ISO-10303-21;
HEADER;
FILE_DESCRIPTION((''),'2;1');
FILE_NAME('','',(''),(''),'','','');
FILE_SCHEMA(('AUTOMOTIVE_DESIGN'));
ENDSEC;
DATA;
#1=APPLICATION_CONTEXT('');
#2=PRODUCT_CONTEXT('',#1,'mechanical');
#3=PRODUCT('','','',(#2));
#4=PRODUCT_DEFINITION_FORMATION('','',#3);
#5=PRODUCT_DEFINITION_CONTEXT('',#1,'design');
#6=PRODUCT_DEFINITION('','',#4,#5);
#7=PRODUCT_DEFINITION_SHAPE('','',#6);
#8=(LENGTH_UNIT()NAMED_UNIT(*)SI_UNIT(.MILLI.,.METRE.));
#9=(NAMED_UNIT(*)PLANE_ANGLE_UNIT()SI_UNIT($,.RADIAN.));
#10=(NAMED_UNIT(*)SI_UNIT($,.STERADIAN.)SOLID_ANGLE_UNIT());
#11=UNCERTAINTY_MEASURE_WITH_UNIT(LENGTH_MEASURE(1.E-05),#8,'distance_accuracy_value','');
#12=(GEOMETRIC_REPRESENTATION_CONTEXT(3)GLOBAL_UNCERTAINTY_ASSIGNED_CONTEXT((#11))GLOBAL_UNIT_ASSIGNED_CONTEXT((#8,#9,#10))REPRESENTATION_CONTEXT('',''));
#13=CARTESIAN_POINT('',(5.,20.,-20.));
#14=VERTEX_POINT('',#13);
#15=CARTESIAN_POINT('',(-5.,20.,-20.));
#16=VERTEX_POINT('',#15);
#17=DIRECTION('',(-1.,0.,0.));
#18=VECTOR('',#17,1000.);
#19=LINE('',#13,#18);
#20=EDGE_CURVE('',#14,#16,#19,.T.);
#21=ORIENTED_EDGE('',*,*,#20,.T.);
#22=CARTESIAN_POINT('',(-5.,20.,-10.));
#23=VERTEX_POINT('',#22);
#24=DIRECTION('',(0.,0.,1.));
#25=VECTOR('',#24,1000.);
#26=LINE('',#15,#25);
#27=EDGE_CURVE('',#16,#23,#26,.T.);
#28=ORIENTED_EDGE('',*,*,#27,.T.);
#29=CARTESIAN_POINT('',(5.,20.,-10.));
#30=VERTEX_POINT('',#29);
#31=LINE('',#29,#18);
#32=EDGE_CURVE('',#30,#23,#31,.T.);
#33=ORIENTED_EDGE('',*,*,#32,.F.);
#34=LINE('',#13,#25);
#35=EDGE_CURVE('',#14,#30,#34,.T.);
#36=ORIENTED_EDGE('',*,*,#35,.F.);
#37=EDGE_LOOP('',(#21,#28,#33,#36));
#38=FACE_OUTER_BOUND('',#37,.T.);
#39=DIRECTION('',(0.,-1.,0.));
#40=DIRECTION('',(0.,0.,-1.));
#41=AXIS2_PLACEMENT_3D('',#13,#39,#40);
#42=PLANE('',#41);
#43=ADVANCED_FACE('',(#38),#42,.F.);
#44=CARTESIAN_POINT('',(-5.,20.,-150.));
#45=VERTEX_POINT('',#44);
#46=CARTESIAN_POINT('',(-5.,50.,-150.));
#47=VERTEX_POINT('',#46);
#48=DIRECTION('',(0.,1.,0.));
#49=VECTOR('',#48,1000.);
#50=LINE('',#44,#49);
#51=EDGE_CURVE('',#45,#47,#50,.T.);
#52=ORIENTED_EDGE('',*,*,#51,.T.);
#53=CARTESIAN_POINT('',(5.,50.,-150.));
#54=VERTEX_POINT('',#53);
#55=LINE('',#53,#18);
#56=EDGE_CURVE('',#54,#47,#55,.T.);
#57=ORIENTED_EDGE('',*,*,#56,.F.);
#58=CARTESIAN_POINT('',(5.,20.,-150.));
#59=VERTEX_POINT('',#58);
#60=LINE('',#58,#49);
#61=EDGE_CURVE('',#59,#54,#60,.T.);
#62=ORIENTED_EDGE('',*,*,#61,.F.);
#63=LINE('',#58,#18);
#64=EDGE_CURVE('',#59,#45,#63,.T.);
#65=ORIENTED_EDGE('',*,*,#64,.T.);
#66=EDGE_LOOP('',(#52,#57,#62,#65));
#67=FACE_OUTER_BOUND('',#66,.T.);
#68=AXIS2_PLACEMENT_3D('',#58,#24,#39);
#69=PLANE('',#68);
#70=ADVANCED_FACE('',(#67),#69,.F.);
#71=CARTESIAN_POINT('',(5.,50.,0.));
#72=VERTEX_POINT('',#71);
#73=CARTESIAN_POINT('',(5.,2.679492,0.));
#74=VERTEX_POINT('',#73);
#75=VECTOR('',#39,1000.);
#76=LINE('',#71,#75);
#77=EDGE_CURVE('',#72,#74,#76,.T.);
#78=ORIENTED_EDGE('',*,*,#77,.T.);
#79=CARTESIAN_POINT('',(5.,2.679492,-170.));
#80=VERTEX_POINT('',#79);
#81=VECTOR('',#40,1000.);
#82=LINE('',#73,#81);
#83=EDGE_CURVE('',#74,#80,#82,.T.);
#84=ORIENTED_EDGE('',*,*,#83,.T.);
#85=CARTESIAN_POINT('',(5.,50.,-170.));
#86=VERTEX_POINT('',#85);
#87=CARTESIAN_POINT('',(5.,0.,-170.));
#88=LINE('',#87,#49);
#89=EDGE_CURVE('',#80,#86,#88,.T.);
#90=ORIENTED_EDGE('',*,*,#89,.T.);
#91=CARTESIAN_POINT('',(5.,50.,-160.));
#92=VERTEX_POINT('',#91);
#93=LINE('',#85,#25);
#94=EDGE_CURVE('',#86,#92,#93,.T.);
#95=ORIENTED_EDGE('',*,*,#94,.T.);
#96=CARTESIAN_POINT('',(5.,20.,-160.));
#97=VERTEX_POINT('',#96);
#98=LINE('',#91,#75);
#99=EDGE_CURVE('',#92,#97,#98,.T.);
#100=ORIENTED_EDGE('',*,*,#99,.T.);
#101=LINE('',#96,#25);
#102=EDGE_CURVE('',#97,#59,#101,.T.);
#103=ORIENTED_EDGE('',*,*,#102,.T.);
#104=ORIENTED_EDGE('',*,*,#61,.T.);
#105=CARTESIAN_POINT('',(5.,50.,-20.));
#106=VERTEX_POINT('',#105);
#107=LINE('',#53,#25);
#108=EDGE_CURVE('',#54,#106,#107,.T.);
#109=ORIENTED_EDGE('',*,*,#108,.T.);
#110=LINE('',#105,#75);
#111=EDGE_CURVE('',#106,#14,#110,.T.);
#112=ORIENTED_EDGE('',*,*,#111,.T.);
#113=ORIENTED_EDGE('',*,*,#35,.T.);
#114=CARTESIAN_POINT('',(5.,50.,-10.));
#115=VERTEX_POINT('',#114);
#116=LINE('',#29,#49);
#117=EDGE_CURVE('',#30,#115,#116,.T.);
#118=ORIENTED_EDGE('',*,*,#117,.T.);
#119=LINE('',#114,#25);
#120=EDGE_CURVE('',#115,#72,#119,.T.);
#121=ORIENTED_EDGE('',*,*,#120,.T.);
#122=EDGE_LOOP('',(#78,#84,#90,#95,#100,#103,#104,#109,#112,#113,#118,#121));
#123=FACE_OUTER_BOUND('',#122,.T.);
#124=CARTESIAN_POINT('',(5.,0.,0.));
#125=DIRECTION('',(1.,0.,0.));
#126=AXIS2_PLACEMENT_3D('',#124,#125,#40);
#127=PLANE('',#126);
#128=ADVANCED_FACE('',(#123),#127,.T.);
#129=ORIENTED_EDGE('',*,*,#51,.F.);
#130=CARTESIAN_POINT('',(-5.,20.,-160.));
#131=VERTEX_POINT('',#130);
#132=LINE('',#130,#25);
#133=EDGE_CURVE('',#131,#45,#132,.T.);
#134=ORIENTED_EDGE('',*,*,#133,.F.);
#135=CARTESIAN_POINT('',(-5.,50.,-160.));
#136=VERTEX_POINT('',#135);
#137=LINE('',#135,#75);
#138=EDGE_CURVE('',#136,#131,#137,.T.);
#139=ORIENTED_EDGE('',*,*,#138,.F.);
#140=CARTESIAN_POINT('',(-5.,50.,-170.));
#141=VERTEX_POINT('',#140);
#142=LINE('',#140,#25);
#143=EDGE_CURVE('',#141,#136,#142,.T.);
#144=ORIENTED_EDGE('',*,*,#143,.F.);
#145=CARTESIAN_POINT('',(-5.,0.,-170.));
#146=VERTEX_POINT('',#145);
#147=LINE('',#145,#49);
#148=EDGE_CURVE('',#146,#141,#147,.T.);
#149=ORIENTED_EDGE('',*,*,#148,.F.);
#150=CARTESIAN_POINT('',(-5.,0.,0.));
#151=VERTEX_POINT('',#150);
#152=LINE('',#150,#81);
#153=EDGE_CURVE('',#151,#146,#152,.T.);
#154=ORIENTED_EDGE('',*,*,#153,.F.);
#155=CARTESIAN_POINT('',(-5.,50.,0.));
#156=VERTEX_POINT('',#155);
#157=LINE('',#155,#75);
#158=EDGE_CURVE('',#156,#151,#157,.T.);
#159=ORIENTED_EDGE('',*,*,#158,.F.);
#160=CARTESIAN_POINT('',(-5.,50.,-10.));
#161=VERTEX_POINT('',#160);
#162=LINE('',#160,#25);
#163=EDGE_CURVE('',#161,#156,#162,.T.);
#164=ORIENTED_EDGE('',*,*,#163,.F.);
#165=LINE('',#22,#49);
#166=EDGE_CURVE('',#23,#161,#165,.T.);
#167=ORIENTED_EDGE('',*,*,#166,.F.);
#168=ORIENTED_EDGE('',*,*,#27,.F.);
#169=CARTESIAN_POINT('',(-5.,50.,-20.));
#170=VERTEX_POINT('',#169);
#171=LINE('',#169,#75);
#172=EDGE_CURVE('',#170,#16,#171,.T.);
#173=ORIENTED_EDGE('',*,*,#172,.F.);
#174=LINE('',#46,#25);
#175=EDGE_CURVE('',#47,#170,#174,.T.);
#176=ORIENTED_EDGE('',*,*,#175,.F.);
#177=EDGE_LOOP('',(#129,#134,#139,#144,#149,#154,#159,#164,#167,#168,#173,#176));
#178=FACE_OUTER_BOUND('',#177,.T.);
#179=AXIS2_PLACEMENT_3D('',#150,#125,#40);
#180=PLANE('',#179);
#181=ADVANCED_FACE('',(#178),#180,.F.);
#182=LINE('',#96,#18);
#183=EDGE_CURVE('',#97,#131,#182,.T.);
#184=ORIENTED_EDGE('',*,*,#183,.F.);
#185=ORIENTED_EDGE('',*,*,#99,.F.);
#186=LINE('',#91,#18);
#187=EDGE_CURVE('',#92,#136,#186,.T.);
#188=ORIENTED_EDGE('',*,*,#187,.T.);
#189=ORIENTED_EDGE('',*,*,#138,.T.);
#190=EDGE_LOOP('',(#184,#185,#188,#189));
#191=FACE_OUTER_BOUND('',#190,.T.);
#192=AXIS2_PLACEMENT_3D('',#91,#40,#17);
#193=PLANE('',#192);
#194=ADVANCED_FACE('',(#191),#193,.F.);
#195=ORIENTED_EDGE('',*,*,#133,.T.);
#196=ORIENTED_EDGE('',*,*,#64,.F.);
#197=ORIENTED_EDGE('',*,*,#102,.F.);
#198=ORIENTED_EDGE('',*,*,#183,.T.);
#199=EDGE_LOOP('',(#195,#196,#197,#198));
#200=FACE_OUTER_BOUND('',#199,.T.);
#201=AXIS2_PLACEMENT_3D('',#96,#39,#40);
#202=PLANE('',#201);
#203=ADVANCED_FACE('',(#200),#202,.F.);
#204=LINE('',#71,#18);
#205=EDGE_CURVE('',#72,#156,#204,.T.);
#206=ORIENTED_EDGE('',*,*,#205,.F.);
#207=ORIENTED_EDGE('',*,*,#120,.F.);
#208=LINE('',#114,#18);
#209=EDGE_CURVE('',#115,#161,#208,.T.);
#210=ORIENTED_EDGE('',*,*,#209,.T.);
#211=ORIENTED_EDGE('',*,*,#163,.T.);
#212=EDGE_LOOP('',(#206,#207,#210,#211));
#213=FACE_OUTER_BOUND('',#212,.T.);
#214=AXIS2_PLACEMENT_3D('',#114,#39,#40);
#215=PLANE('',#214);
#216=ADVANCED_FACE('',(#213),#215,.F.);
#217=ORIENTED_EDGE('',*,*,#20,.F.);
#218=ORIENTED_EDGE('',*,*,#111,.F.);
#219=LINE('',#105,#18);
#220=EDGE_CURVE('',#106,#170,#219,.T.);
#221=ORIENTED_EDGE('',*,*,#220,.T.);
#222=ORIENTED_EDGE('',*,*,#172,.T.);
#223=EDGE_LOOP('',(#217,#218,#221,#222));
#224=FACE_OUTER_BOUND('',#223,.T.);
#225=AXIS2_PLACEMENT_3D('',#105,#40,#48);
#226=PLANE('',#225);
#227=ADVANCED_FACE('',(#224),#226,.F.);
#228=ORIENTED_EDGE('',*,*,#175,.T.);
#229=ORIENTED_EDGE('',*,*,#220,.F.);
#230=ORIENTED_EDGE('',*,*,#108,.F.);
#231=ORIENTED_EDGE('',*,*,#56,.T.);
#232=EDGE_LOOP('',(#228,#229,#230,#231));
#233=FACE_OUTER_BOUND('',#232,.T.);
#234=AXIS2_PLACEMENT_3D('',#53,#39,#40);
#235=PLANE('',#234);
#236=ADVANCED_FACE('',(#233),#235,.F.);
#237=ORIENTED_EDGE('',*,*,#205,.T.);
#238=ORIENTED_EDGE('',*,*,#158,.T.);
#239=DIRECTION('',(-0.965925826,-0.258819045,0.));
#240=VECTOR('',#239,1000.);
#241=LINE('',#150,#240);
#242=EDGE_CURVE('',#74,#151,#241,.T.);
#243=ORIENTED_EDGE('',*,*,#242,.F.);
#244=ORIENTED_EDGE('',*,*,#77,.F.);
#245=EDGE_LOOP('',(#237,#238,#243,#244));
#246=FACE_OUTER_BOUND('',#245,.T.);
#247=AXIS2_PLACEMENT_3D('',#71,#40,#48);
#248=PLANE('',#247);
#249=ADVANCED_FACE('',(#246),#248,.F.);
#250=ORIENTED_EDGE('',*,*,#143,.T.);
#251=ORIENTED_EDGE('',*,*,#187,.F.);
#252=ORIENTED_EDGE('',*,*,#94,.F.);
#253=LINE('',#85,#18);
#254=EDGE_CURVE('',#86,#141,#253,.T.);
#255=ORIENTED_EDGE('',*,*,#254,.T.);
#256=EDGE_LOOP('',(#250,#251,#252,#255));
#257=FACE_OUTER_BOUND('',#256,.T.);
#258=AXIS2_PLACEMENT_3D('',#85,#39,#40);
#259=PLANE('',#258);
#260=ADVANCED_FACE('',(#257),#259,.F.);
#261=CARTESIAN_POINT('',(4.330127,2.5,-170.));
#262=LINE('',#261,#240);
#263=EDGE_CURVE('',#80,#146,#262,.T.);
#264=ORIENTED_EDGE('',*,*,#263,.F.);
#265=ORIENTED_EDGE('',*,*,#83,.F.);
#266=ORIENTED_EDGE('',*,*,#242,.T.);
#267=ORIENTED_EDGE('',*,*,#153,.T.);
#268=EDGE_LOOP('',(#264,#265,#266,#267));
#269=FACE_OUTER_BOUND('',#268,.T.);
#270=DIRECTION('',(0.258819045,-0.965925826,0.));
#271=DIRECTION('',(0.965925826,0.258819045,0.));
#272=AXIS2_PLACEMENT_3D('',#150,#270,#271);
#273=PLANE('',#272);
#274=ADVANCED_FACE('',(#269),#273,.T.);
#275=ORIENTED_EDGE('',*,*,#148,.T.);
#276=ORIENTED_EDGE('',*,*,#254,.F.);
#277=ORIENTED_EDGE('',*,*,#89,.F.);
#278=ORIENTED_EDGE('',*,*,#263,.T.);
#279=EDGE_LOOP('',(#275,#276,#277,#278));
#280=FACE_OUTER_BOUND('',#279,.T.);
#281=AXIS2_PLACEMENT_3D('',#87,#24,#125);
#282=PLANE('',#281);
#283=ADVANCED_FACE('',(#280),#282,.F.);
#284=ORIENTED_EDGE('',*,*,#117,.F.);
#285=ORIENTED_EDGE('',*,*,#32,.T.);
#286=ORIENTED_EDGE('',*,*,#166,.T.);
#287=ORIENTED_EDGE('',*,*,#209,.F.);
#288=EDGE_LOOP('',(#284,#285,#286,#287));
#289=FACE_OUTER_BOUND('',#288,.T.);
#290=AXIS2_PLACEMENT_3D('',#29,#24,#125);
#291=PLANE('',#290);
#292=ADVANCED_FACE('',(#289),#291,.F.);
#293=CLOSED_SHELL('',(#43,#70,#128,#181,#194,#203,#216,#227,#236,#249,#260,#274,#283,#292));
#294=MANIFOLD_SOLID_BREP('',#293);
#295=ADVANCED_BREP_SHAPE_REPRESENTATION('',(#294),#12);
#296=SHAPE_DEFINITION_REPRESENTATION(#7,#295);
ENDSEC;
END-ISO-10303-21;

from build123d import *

# Parameters (mm, degrees)
STEP_PLATE_10MM_DEPTH = 5
DRAFT_15DEG_ANGLE     = -15


with BuildPart() as part:
    # Step Plate Profile → Step Plate 10mm (new, symmetric)
    with BuildSketch(Plane(origin=(0, 0, 0), x_dir=(0, 0, -1), z_dir=(1, 0, 0))):
        Polygon((0, 0), (170, 0), (170, 50), (160, 50), (160, 20), (150, 20), (150, 50), (20, 50), (20, 20), (10, 20), (10, 50), (0, 50), align=None)
    extrude(amount=STEP_PLATE_10MM_DEPTH, both=True)

    # Draft 15deg
    draft_15deg_faces = [part.faces().sort_by_distance(p)[0] for p in [
        (0, 0, -85),
    ]]
    draft(draft_15deg_faces, Plane(origin=(-5, 0, 0), x_dir=(0, 0, -1), z_dir=(-1, 0, 0)), DRAFT_15DEG_ANGLE)


solid = part.part
